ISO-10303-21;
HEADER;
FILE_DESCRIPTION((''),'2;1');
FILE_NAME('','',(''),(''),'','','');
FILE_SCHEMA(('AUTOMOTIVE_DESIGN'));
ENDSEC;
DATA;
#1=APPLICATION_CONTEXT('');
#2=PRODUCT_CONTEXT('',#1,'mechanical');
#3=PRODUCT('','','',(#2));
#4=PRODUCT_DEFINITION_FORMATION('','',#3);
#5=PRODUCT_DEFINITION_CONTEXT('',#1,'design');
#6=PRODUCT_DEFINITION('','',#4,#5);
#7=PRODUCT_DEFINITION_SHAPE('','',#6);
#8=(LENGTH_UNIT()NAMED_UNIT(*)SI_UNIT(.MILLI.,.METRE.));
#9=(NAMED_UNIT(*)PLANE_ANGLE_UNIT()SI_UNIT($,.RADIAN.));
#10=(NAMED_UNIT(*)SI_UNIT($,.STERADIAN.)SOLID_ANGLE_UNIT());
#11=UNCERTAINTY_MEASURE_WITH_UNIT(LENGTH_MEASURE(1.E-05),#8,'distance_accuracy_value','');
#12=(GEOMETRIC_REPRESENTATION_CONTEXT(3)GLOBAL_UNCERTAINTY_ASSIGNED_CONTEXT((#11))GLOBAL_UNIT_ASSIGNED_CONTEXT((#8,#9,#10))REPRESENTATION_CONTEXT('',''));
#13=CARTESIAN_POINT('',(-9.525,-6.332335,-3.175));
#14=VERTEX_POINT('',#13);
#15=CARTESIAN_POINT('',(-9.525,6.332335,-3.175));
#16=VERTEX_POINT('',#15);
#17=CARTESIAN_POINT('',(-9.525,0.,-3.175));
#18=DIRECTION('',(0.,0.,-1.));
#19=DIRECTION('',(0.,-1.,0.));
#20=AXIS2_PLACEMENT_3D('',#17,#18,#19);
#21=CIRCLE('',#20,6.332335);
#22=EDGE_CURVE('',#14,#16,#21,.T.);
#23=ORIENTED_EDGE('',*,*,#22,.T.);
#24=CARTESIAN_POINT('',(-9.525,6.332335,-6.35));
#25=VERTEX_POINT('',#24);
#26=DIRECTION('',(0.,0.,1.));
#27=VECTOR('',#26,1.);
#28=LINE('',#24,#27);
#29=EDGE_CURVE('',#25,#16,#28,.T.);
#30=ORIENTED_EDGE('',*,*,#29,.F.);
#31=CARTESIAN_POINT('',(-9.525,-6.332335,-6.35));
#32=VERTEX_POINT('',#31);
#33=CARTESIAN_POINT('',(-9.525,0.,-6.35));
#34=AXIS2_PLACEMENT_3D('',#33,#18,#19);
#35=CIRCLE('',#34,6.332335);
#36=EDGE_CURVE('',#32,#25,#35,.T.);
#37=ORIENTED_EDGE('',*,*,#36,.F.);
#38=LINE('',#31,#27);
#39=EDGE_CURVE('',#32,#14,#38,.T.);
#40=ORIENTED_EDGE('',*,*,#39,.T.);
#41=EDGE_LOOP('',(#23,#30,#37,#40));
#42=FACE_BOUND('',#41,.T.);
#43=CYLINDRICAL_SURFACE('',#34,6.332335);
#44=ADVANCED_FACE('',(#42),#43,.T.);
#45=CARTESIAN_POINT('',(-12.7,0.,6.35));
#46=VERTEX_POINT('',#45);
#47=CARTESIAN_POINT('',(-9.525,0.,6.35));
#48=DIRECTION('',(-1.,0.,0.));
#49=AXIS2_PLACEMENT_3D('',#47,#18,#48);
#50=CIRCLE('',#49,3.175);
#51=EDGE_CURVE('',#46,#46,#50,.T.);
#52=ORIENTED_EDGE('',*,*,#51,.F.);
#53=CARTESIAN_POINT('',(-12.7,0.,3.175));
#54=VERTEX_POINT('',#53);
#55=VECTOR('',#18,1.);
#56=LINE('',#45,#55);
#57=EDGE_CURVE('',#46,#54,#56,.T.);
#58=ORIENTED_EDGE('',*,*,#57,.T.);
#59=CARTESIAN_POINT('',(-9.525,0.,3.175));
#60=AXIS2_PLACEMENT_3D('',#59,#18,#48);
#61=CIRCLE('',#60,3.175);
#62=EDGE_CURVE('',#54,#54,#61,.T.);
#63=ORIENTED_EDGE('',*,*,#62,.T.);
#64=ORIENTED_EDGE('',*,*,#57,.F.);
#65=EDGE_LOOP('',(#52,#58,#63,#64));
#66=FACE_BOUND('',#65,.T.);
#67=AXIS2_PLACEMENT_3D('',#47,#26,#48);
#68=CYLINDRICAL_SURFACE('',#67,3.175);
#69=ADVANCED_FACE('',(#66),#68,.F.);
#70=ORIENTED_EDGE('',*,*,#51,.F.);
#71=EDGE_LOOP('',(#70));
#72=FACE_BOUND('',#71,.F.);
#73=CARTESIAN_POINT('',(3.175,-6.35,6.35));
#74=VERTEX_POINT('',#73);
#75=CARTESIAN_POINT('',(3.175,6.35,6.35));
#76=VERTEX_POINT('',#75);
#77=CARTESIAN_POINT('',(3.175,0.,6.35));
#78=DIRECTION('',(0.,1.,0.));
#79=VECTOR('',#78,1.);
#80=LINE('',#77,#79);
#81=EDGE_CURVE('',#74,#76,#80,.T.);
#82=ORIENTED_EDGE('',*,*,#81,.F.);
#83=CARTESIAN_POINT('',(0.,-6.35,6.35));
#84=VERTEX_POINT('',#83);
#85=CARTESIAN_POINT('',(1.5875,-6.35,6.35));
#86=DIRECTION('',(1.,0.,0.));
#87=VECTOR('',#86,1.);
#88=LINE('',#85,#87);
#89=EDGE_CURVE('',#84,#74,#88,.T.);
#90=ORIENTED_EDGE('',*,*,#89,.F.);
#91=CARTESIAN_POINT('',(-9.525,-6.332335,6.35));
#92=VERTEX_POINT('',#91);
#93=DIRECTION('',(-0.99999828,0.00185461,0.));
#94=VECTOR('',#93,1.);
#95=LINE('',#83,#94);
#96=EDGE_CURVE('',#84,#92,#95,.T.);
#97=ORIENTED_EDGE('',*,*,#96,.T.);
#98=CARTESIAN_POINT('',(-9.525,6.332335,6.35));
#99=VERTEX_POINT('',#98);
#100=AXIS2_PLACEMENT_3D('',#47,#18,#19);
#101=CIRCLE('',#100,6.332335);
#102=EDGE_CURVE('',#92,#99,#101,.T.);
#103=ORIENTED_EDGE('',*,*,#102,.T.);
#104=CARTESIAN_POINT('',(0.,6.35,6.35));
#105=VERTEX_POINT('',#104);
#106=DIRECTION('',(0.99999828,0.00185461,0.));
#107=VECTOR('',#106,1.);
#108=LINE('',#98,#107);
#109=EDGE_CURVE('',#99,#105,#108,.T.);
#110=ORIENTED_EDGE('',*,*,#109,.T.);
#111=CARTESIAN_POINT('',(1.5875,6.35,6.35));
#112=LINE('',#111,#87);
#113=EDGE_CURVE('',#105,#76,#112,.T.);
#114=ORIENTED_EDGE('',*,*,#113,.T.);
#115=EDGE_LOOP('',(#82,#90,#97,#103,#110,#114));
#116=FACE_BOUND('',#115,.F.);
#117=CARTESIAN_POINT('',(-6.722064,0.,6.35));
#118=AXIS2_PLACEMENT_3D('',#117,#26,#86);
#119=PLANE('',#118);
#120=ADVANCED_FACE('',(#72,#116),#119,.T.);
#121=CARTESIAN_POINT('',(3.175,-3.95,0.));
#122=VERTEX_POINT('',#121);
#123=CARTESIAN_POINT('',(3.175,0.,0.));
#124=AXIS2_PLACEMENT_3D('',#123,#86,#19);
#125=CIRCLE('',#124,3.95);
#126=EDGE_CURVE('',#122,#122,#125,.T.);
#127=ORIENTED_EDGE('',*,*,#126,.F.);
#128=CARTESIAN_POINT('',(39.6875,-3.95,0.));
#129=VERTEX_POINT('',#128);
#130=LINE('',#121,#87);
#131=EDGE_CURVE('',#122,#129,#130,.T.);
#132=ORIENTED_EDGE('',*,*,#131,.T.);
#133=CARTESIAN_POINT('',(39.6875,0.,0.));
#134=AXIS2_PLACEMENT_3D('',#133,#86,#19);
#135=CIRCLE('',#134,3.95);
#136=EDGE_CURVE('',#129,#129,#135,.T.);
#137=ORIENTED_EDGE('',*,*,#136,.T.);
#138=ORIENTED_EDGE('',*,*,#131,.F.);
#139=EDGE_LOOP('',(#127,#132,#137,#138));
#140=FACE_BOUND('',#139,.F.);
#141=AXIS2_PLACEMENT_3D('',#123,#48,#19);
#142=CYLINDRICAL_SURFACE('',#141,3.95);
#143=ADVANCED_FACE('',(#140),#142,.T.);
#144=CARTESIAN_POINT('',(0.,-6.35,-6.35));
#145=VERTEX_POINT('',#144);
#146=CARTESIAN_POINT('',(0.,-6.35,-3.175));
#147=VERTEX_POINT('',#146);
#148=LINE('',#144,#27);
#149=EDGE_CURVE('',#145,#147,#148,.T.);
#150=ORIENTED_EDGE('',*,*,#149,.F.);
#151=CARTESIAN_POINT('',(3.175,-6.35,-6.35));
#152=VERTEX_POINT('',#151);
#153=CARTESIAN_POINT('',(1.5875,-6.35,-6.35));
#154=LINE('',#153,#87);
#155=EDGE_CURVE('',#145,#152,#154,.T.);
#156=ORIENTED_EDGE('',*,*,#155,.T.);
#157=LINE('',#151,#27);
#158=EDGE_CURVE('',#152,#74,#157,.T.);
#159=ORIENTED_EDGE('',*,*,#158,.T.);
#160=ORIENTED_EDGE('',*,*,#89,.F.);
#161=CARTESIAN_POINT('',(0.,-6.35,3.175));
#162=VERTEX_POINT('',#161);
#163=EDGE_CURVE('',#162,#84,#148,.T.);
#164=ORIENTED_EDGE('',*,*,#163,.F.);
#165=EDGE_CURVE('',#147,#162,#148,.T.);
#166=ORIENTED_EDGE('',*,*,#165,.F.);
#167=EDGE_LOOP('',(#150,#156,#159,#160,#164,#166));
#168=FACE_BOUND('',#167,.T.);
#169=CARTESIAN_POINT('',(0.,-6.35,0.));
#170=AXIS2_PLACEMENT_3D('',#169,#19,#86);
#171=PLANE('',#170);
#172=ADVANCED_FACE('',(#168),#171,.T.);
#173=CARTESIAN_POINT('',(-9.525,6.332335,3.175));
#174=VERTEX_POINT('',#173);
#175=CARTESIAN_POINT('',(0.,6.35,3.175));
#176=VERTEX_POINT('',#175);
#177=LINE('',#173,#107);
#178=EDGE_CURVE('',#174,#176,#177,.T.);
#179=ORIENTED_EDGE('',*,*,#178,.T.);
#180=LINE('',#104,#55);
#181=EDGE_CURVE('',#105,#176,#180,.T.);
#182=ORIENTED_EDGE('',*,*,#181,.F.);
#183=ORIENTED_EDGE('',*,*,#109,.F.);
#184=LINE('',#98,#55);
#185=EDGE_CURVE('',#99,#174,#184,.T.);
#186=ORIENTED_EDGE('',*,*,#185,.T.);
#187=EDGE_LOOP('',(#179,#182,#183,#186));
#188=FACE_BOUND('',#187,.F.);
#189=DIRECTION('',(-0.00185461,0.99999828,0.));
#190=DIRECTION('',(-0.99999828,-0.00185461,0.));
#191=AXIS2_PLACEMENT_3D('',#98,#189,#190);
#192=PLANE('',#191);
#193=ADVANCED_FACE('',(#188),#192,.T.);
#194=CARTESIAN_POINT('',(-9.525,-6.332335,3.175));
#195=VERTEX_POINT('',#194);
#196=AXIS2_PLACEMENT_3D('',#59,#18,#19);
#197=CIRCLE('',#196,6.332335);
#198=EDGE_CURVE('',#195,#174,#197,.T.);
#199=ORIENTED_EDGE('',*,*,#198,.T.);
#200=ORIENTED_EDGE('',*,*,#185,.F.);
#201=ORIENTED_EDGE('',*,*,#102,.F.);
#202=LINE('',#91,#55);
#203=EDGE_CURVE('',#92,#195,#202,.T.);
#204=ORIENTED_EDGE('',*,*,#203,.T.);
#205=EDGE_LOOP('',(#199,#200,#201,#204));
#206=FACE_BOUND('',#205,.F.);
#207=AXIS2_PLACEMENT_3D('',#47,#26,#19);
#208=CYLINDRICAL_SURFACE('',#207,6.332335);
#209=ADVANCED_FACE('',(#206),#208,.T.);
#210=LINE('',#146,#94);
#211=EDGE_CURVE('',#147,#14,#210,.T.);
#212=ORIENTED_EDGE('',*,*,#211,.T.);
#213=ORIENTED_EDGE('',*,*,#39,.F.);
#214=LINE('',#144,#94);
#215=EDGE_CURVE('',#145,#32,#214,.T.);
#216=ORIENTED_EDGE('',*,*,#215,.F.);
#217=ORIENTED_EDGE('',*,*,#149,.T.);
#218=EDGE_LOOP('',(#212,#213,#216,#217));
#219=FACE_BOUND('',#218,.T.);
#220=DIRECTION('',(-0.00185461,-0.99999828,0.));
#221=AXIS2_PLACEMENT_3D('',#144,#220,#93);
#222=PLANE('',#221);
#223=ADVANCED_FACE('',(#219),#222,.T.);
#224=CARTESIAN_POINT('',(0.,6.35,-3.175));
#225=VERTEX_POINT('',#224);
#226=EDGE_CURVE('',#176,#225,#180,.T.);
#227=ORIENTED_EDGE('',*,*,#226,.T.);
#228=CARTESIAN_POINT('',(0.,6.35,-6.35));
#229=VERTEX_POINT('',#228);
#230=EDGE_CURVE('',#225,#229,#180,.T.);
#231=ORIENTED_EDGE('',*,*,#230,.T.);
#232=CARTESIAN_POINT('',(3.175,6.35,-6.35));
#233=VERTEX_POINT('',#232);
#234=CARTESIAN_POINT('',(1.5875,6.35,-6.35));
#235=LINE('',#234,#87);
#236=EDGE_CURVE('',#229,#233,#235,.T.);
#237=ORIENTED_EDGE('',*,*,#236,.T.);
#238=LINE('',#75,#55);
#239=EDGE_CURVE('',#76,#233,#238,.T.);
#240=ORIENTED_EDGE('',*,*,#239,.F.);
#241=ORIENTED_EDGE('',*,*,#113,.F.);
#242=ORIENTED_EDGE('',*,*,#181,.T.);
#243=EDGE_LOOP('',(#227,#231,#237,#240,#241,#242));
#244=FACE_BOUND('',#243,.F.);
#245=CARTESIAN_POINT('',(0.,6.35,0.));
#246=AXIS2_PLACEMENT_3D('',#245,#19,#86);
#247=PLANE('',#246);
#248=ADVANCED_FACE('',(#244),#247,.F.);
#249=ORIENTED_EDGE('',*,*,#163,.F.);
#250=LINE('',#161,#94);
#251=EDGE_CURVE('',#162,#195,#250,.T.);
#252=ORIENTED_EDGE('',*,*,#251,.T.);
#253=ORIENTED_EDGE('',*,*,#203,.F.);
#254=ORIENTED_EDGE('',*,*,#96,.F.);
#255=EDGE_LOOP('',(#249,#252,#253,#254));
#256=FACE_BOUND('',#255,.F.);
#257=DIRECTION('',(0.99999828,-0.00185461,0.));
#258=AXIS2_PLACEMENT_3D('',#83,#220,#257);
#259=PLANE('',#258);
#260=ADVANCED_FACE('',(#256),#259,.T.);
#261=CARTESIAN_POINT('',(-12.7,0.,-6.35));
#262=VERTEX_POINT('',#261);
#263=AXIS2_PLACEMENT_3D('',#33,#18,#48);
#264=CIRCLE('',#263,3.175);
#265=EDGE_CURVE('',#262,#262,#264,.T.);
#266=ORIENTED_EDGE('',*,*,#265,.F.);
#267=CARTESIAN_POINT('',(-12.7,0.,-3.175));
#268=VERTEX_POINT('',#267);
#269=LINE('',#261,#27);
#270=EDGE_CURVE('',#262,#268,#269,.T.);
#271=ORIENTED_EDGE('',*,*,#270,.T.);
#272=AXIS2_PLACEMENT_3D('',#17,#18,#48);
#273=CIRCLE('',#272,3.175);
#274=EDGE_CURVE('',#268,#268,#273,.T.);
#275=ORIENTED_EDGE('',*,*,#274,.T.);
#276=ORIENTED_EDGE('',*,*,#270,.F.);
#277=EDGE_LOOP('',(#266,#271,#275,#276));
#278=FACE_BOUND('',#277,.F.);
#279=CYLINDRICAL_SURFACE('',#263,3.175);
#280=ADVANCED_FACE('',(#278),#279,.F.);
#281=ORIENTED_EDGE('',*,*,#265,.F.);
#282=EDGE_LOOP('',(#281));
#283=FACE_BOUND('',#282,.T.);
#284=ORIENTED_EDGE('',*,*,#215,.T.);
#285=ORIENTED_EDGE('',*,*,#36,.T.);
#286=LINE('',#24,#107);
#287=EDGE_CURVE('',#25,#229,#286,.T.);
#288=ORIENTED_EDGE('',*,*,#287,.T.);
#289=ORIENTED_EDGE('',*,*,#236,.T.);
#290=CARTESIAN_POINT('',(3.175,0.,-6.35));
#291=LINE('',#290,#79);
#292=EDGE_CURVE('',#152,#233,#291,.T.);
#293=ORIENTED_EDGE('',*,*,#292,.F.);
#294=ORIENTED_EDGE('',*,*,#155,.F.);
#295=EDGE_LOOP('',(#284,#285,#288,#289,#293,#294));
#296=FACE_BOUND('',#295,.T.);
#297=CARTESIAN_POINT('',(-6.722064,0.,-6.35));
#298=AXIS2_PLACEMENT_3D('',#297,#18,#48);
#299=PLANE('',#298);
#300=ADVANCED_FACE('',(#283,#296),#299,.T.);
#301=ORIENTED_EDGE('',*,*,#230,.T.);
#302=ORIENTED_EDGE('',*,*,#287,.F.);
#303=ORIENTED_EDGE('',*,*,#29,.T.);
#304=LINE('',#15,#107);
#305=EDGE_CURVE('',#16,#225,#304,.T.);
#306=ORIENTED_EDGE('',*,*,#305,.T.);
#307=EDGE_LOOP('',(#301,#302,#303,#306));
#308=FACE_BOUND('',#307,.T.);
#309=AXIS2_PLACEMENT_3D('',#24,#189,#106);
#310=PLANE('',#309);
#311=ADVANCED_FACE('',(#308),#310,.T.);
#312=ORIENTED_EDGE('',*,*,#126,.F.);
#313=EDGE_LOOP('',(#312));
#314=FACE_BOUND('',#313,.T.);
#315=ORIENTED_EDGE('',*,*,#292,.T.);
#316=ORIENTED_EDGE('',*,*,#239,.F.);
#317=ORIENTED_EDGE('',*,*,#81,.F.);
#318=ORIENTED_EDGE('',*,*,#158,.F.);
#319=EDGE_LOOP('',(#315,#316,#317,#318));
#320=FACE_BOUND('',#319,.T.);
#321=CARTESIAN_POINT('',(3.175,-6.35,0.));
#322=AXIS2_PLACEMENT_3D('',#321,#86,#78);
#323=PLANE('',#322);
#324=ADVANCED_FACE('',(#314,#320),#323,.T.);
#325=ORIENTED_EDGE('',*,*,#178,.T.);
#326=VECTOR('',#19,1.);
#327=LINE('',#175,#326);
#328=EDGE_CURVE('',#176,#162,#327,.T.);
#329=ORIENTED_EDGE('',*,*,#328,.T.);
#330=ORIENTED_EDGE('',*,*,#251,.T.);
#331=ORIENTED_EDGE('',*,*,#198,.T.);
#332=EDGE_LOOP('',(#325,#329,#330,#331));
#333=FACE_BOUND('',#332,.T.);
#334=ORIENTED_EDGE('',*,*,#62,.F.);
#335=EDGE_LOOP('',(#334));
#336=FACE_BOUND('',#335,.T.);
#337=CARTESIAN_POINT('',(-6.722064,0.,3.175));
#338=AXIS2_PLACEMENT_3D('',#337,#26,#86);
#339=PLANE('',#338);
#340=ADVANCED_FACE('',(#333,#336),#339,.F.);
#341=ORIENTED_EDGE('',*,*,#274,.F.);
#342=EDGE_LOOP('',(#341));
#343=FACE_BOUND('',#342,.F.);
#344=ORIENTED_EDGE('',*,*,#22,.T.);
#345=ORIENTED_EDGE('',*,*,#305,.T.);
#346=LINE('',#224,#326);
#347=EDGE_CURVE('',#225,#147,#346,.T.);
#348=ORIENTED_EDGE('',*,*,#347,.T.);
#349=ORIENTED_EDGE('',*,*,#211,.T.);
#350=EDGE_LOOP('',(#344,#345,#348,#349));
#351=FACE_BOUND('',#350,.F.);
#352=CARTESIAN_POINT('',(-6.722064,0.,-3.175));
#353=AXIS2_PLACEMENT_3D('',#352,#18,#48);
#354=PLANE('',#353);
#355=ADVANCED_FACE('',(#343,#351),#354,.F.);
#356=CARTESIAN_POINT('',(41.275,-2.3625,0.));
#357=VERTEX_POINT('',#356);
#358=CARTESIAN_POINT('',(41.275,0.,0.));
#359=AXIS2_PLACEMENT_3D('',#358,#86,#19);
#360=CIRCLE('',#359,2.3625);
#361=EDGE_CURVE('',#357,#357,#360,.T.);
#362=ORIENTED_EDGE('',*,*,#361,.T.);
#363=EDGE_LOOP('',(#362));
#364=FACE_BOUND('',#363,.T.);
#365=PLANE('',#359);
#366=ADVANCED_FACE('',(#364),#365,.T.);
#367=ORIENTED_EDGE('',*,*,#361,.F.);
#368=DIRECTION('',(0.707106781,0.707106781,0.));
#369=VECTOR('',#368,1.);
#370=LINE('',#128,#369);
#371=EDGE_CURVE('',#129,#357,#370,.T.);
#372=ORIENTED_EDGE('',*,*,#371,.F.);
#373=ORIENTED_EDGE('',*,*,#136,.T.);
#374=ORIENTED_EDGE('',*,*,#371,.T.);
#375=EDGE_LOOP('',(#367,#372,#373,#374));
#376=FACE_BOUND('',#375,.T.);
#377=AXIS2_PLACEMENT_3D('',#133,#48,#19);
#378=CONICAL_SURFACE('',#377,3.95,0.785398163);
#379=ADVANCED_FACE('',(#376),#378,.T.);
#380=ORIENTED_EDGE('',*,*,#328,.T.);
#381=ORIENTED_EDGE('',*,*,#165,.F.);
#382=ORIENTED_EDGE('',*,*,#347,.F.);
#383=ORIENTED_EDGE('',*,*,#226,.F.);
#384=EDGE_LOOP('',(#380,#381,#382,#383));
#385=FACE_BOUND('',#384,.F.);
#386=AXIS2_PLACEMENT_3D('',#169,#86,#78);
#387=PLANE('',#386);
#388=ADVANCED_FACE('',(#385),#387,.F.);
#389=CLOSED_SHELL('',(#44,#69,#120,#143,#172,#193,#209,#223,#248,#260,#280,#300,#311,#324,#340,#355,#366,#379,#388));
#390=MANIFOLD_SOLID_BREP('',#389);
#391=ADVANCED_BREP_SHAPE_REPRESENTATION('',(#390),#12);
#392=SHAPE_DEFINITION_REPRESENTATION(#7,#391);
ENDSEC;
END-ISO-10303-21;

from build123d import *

# Parameters (mm, degrees)
CLEVIS_BLOCK_SKETCH_W  = 3.175
CLEVIS_BLOCK_SKETCH_H  = 12.7
CLEVIS_BLOCK_DEPTH     = 6.35
SHANK_SKETCH_7_95_R    = 3.95
SHANK_7_95_DEPTH       = 38.1
SHANK_END_CHAMFER_SIZE = 1.5875
CLEVIS_EAR_SKETCH_R    = 3.175
CLEVIS_EAR_DEPTH       = 3.175


with BuildPart() as part:
    # Clevis Block Sketch → Clevis Block (new, symmetric)
    with BuildSketch(Plane.XY):
        with Locations((1.5875, 0)):
            Rectangle(CLEVIS_BLOCK_SKETCH_W, CLEVIS_BLOCK_SKETCH_H)
    extrude(amount=CLEVIS_BLOCK_DEPTH, both=True)

    # Shank Sketch Ø7.95 → Shank Ø7.95 (add)
    with BuildSketch(Plane(origin=(3.175, 0, 0), x_dir=(0, 0, -1), z_dir=(1, 0, 0))):
        with Locations(Location((0, 0, 0), (0, 0, 270))):
            Circle(SHANK_SKETCH_7_95_R)
    extrude(amount=SHANK_7_95_DEPTH)

    # Shank End Chamfer
    shank_end_chamfer_edges = [part.edges().sort_by_distance(p)[0] for p in [
        (41.275, 3.95, 0),
    ]]
    chamfer(shank_end_chamfer_edges, length=SHANK_END_CHAMFER_SIZE)

    # Clevis Ear Sketch → Clevis Ear (add)
    with BuildSketch(Plane(origin=(0, 0, -6.35), x_dir=(-1, 0, 0), z_dir=(0, 0, -1))):
        with BuildLine():
            Line((9.525, 6.332334812), (0, 6.35))
            Line((0, 6.35), (0, -6.35))
            Line((0, -6.35), (9.525, -6.332334812))
            ThreePointArc((9.525, -6.332334812), (15.857334812, 0), (9.525, 6.332334812))
        make_face()
        with Locations((9.525, 0)):
            Circle(CLEVIS_EAR_SKETCH_R, mode=Mode.SUBTRACT)
    clevis_ear = extrude(amount=-CLEVIS_EAR_DEPTH)

    # Clevis Ear Mirror: Clevis Ear across plane
    add(clevis_ear.mirror(Plane.XY))


solid = part.part
